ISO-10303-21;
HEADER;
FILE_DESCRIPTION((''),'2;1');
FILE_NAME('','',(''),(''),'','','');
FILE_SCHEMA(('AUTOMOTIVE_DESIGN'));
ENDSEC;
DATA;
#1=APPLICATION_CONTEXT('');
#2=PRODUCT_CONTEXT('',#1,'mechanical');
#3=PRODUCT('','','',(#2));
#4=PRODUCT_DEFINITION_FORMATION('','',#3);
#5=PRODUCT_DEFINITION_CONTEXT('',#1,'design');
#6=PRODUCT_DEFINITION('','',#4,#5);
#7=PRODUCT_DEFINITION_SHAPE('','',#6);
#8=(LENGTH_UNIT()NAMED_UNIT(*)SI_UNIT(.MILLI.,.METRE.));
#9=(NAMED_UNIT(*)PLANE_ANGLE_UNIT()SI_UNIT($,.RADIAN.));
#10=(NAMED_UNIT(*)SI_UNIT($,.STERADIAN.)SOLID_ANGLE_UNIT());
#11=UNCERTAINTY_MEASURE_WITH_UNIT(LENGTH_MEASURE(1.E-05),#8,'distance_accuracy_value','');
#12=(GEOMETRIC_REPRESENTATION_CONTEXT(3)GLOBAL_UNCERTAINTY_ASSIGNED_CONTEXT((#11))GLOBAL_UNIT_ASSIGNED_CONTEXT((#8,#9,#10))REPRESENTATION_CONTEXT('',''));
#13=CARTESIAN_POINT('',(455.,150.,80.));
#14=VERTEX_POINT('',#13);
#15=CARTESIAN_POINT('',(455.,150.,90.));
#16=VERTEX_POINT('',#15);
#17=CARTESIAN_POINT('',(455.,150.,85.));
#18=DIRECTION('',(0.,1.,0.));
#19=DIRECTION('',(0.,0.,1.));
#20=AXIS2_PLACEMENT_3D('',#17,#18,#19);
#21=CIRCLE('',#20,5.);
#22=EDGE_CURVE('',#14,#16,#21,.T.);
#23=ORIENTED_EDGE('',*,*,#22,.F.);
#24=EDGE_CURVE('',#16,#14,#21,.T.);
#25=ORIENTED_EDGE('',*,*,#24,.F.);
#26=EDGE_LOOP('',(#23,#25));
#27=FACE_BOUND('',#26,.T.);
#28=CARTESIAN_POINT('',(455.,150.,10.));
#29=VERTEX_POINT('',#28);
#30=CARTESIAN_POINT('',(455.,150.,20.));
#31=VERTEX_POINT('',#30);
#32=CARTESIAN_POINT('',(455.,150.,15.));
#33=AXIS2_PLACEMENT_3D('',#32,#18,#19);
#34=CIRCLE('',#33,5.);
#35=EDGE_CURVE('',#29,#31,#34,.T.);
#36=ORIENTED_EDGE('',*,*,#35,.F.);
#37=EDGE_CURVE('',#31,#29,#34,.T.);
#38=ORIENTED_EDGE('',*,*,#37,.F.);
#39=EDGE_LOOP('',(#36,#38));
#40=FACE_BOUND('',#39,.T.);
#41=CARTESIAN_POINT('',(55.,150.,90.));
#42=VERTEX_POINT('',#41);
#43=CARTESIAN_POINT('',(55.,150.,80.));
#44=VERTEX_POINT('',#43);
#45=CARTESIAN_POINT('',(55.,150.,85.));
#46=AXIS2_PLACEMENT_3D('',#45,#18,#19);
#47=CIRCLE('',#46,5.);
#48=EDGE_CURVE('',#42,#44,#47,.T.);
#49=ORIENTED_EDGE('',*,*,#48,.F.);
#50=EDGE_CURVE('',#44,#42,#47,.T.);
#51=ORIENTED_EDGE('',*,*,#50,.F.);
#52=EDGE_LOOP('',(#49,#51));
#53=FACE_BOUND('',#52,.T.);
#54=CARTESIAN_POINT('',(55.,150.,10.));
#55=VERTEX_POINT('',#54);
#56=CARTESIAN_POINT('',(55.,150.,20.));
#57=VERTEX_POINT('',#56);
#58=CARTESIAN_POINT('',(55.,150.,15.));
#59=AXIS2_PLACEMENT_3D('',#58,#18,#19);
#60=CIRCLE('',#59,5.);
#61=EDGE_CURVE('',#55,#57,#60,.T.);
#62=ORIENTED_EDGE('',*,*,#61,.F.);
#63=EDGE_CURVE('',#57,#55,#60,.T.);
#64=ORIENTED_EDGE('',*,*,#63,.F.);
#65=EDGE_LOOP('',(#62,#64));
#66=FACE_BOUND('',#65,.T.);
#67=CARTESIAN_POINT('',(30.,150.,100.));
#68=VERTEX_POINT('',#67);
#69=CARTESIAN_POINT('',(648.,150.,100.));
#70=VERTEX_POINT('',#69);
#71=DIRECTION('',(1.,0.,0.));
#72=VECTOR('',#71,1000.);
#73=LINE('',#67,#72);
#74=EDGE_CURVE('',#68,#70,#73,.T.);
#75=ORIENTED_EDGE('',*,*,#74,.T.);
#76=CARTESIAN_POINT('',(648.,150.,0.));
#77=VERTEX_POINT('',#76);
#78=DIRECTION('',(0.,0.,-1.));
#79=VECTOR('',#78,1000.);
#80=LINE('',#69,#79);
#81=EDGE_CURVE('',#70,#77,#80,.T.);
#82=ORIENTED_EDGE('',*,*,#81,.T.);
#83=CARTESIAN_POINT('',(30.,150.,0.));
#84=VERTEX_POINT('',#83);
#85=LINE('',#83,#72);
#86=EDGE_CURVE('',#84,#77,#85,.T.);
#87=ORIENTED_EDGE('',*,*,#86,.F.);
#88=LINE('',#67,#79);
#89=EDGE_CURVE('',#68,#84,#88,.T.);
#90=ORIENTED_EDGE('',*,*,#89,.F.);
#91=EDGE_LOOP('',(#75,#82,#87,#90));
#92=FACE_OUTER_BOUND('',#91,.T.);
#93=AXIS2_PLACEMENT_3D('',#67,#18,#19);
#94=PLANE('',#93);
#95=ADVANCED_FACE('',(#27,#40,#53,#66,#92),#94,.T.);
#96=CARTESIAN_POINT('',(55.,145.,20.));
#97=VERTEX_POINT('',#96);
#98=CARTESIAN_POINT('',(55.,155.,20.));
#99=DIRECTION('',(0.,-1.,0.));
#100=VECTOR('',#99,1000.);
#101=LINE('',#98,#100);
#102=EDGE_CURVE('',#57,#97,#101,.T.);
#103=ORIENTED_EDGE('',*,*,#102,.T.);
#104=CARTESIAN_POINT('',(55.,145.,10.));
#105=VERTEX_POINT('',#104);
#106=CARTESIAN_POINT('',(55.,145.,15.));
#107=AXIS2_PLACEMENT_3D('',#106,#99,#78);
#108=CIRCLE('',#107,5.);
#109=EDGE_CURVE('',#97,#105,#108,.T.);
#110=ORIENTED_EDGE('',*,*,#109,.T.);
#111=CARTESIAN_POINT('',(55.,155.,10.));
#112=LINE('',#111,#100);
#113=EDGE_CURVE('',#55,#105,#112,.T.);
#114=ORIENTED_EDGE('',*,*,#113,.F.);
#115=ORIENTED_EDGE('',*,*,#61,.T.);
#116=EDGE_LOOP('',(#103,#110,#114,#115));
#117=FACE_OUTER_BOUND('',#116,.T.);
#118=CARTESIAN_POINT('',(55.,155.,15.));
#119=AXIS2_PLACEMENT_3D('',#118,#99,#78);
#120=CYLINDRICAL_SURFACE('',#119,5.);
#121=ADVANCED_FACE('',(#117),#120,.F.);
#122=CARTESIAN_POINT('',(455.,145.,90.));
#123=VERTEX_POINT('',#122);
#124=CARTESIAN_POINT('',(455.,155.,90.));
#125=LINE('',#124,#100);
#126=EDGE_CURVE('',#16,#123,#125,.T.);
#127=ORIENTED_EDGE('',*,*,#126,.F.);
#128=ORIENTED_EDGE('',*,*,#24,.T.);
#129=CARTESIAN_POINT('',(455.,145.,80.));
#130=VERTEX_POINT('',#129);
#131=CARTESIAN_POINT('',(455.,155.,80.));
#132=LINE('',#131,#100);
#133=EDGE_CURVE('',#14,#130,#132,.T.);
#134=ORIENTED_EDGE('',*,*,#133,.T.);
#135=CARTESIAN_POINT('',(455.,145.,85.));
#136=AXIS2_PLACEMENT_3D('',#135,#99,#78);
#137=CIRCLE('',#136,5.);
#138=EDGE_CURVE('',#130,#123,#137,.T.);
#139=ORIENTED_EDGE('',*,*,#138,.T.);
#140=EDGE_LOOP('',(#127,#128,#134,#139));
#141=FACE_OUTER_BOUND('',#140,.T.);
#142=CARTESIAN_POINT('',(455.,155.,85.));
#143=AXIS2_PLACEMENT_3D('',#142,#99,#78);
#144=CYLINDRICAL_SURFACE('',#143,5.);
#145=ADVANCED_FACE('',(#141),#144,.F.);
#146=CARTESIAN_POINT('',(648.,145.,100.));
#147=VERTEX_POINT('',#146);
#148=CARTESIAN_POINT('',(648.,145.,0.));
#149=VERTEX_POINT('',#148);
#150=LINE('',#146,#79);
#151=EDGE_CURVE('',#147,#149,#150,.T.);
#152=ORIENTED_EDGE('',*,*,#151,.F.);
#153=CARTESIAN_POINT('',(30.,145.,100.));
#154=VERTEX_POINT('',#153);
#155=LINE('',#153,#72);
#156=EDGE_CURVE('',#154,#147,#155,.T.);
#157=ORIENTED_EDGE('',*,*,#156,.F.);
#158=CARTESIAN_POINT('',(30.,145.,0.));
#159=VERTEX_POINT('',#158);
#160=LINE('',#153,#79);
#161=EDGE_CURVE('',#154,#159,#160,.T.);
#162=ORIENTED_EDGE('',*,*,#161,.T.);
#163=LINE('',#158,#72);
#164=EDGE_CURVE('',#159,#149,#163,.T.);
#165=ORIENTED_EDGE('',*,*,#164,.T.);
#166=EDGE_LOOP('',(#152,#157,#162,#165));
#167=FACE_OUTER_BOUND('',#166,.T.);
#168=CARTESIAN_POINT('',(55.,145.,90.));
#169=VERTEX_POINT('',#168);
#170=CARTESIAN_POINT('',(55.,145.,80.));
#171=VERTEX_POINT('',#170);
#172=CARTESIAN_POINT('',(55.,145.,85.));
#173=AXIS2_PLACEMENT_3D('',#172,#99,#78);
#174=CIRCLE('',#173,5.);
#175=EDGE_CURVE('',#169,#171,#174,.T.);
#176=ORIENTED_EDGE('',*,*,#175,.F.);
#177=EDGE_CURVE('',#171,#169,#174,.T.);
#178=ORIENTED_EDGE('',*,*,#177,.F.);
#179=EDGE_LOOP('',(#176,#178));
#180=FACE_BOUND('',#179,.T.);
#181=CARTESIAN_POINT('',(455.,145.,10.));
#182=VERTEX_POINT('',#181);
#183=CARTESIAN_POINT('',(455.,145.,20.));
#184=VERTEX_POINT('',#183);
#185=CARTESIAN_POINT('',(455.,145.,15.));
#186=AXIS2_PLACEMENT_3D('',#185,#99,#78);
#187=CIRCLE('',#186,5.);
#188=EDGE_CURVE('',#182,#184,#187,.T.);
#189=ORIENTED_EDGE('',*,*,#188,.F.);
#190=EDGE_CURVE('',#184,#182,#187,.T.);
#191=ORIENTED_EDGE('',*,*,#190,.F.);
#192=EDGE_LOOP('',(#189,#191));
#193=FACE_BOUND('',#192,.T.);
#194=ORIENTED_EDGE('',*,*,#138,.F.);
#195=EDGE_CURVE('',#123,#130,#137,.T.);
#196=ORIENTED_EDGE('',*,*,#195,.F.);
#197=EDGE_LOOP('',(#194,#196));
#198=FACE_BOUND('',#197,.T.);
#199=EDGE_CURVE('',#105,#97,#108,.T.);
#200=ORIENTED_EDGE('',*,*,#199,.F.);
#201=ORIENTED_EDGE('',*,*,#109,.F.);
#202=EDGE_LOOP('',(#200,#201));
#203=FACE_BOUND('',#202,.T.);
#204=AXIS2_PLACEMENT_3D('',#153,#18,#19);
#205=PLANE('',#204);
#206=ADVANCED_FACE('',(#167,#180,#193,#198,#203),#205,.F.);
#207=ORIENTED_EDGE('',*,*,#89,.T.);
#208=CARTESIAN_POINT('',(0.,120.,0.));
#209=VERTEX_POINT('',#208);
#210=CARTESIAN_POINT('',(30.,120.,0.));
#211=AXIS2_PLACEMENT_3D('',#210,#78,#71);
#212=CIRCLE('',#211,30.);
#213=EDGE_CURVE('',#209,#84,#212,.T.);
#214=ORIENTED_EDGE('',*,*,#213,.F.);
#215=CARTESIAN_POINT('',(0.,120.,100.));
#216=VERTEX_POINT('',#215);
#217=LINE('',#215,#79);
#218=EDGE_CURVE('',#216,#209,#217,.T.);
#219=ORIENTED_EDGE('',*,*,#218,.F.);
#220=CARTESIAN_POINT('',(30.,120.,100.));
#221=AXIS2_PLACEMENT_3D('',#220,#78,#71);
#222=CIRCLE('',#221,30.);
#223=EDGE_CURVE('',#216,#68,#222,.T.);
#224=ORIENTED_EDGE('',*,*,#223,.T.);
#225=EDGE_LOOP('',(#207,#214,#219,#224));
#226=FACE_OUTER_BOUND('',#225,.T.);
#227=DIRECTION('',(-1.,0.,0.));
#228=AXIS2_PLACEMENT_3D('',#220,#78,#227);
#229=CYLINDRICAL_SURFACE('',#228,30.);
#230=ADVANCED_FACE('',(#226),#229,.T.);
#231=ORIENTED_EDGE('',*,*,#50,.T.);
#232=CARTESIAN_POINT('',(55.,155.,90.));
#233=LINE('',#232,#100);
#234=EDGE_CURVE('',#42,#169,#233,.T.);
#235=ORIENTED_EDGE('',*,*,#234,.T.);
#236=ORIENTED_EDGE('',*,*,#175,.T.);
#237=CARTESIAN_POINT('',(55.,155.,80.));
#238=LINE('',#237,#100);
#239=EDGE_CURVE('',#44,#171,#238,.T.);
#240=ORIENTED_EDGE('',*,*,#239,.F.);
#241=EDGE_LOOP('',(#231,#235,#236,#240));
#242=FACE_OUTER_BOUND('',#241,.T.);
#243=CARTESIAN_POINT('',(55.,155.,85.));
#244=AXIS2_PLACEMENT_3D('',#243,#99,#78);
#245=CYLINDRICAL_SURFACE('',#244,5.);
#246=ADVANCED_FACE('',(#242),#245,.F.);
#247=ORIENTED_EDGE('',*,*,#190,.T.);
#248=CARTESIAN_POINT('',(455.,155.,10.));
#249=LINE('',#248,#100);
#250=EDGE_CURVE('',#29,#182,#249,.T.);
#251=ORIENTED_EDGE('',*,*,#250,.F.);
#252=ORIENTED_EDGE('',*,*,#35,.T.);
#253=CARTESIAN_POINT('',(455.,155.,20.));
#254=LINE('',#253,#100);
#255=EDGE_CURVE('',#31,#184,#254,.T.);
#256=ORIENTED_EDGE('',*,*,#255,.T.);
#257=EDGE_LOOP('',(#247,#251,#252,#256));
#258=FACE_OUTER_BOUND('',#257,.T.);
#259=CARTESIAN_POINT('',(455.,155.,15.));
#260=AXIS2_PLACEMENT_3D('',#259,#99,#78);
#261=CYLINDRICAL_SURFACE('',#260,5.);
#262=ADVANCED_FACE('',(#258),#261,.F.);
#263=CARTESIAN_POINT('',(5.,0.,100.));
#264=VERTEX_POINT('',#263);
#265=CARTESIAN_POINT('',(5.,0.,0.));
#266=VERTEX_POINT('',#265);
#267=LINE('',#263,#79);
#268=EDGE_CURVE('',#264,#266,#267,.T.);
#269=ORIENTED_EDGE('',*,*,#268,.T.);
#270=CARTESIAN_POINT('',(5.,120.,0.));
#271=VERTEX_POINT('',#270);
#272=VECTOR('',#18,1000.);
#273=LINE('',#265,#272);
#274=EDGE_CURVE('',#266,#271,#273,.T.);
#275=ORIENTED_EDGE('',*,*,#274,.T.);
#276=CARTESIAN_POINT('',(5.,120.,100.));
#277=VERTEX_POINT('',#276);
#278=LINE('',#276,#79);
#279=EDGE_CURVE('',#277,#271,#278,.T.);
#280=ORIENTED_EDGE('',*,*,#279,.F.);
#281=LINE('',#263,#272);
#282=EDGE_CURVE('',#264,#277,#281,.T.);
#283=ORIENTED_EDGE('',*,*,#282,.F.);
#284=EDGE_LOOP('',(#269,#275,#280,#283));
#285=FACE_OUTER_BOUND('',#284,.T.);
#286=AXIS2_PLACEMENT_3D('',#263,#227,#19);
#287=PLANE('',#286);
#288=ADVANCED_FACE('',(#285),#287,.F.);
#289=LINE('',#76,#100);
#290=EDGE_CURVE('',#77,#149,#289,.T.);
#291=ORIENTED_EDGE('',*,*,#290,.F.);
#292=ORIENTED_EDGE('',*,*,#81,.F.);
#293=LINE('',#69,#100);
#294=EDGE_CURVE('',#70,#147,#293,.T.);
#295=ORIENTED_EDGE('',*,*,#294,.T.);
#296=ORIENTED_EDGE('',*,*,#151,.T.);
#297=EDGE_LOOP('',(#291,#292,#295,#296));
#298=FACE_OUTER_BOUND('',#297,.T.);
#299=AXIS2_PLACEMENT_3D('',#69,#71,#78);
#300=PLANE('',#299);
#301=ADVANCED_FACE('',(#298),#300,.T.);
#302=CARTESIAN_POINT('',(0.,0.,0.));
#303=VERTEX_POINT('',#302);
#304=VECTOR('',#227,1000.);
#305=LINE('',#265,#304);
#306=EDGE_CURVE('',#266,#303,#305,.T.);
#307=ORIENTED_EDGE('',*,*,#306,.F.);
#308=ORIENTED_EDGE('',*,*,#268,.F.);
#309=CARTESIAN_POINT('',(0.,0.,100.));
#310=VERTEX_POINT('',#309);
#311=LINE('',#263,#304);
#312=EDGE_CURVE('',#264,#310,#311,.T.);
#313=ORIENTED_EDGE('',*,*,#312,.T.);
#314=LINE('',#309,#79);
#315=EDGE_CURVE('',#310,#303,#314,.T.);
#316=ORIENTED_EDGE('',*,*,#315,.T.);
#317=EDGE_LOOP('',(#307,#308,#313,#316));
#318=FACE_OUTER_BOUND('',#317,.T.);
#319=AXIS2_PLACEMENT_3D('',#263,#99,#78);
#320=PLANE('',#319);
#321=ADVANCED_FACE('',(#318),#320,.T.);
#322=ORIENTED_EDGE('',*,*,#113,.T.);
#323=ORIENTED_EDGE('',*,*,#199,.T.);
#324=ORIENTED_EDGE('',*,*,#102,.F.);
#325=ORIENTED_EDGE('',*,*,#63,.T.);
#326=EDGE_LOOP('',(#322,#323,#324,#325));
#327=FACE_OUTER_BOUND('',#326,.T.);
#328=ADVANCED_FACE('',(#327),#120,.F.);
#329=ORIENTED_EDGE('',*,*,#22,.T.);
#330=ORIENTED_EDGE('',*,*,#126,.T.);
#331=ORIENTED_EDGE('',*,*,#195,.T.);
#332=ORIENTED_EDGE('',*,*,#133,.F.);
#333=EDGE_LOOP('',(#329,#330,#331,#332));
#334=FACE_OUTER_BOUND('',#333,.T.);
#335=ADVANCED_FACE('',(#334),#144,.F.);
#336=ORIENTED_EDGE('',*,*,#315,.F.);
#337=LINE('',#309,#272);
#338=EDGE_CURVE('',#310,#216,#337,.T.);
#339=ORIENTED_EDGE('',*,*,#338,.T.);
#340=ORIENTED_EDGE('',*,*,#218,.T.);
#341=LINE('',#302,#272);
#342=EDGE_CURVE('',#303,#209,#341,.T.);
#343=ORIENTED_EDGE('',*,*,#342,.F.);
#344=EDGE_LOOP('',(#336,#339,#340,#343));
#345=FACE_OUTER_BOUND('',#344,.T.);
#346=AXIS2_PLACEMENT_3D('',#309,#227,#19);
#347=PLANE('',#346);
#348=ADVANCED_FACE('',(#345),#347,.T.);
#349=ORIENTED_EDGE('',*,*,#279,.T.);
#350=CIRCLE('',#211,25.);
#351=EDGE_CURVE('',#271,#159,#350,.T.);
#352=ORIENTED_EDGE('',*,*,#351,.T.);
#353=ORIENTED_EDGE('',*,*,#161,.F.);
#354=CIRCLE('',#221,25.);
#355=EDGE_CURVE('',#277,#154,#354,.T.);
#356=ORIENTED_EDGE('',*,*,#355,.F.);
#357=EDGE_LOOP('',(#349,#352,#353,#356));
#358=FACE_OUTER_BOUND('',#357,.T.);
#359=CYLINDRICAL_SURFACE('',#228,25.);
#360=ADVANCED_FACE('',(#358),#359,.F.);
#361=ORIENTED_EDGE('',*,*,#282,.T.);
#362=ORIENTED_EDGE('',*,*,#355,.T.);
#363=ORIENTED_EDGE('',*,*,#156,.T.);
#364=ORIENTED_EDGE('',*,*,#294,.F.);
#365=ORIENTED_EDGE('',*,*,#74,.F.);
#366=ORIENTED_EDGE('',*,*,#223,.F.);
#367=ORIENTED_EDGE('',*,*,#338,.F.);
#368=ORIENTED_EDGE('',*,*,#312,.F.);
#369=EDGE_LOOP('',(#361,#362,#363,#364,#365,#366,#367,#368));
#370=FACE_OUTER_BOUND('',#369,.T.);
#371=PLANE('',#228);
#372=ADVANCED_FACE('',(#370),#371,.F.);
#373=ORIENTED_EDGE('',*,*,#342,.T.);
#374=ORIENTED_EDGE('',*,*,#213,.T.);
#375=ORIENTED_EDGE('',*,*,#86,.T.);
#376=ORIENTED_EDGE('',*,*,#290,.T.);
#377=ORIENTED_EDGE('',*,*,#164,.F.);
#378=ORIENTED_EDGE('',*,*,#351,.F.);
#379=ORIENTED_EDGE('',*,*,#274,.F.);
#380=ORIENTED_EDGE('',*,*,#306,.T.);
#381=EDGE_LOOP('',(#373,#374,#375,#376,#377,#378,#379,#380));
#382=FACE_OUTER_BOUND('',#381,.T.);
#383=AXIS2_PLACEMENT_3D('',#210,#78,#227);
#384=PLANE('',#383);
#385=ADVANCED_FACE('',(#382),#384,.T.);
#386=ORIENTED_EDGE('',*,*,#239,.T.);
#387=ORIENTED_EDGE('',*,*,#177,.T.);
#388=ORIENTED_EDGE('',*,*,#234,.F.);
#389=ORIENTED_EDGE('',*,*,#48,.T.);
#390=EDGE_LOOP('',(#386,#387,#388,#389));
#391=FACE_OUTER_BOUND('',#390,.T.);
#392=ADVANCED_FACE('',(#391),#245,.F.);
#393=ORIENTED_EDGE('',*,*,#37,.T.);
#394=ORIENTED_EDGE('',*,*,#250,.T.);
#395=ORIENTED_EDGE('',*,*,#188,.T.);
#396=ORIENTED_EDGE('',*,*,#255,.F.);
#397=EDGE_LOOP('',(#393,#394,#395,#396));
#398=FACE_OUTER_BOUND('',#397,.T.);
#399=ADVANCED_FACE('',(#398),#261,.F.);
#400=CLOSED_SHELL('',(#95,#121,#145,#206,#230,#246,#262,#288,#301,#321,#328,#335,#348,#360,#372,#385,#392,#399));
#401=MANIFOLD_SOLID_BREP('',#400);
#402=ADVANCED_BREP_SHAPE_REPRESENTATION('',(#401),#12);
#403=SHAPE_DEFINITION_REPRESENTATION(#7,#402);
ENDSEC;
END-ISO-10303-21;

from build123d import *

# Parameters (mm, degrees)
EXTRUDE_THIN1_DEPTH  = 100
SKETCH2_R            = 5
CUT_EXTRUDE1_DEPTH   = 10
LPATTERN1_COUNT      = 2
LPATTERN1_PITCH      = 400
LPATTERN1_COUNT_DIR2 = 2
LPATTERN1_PITCH_DIR2 = 70


with BuildPart() as part:
    # Sketch1 → Extrude-Thin1 (new body)
    with BuildSketch(Plane.XY):
        with BuildLine():
            Line((0, 0), (0, 120))
            ThreePointArc((0, 120), (8.786796564, 141.213203436), (30, 150))
            Line((30, 150), (648, 150))
            Line((648, 150), (648, 145))
            Line((648, 145), (30, 145))
            ThreePointArc((30, 145), (12.32233047, 137.67766953), (5, 120))
            Line((5, 120), (5, 0))
            Line((5, 0), (0, 0))
        make_face()
    extrude(amount=EXTRUDE_THIN1_DEPTH)

    # Sketch2 → Cut-Extrude1 (cut)
    with BuildSketch(Plane.XZ.offset(-145)):
        with Locations(Location((55, 85, 0), (0, 0, 270))):
            Circle(SKETCH2_R)
    cut_extrude1 = extrude(amount=-CUT_EXTRUDE1_DEPTH, mode=Mode.SUBTRACT)

    # LPattern1: Cut-Extrude1 2 × 2
    with Locations(*[(i * LPATTERN1_PITCH, 0, -j * LPATTERN1_PITCH_DIR2) for i in range(LPATTERN1_COUNT) for j in range(LPATTERN1_COUNT_DIR2) if (i, j) != (0, 0)]):
        add(cut_extrude1, mode=Mode.SUBTRACT)


solid = part.part
